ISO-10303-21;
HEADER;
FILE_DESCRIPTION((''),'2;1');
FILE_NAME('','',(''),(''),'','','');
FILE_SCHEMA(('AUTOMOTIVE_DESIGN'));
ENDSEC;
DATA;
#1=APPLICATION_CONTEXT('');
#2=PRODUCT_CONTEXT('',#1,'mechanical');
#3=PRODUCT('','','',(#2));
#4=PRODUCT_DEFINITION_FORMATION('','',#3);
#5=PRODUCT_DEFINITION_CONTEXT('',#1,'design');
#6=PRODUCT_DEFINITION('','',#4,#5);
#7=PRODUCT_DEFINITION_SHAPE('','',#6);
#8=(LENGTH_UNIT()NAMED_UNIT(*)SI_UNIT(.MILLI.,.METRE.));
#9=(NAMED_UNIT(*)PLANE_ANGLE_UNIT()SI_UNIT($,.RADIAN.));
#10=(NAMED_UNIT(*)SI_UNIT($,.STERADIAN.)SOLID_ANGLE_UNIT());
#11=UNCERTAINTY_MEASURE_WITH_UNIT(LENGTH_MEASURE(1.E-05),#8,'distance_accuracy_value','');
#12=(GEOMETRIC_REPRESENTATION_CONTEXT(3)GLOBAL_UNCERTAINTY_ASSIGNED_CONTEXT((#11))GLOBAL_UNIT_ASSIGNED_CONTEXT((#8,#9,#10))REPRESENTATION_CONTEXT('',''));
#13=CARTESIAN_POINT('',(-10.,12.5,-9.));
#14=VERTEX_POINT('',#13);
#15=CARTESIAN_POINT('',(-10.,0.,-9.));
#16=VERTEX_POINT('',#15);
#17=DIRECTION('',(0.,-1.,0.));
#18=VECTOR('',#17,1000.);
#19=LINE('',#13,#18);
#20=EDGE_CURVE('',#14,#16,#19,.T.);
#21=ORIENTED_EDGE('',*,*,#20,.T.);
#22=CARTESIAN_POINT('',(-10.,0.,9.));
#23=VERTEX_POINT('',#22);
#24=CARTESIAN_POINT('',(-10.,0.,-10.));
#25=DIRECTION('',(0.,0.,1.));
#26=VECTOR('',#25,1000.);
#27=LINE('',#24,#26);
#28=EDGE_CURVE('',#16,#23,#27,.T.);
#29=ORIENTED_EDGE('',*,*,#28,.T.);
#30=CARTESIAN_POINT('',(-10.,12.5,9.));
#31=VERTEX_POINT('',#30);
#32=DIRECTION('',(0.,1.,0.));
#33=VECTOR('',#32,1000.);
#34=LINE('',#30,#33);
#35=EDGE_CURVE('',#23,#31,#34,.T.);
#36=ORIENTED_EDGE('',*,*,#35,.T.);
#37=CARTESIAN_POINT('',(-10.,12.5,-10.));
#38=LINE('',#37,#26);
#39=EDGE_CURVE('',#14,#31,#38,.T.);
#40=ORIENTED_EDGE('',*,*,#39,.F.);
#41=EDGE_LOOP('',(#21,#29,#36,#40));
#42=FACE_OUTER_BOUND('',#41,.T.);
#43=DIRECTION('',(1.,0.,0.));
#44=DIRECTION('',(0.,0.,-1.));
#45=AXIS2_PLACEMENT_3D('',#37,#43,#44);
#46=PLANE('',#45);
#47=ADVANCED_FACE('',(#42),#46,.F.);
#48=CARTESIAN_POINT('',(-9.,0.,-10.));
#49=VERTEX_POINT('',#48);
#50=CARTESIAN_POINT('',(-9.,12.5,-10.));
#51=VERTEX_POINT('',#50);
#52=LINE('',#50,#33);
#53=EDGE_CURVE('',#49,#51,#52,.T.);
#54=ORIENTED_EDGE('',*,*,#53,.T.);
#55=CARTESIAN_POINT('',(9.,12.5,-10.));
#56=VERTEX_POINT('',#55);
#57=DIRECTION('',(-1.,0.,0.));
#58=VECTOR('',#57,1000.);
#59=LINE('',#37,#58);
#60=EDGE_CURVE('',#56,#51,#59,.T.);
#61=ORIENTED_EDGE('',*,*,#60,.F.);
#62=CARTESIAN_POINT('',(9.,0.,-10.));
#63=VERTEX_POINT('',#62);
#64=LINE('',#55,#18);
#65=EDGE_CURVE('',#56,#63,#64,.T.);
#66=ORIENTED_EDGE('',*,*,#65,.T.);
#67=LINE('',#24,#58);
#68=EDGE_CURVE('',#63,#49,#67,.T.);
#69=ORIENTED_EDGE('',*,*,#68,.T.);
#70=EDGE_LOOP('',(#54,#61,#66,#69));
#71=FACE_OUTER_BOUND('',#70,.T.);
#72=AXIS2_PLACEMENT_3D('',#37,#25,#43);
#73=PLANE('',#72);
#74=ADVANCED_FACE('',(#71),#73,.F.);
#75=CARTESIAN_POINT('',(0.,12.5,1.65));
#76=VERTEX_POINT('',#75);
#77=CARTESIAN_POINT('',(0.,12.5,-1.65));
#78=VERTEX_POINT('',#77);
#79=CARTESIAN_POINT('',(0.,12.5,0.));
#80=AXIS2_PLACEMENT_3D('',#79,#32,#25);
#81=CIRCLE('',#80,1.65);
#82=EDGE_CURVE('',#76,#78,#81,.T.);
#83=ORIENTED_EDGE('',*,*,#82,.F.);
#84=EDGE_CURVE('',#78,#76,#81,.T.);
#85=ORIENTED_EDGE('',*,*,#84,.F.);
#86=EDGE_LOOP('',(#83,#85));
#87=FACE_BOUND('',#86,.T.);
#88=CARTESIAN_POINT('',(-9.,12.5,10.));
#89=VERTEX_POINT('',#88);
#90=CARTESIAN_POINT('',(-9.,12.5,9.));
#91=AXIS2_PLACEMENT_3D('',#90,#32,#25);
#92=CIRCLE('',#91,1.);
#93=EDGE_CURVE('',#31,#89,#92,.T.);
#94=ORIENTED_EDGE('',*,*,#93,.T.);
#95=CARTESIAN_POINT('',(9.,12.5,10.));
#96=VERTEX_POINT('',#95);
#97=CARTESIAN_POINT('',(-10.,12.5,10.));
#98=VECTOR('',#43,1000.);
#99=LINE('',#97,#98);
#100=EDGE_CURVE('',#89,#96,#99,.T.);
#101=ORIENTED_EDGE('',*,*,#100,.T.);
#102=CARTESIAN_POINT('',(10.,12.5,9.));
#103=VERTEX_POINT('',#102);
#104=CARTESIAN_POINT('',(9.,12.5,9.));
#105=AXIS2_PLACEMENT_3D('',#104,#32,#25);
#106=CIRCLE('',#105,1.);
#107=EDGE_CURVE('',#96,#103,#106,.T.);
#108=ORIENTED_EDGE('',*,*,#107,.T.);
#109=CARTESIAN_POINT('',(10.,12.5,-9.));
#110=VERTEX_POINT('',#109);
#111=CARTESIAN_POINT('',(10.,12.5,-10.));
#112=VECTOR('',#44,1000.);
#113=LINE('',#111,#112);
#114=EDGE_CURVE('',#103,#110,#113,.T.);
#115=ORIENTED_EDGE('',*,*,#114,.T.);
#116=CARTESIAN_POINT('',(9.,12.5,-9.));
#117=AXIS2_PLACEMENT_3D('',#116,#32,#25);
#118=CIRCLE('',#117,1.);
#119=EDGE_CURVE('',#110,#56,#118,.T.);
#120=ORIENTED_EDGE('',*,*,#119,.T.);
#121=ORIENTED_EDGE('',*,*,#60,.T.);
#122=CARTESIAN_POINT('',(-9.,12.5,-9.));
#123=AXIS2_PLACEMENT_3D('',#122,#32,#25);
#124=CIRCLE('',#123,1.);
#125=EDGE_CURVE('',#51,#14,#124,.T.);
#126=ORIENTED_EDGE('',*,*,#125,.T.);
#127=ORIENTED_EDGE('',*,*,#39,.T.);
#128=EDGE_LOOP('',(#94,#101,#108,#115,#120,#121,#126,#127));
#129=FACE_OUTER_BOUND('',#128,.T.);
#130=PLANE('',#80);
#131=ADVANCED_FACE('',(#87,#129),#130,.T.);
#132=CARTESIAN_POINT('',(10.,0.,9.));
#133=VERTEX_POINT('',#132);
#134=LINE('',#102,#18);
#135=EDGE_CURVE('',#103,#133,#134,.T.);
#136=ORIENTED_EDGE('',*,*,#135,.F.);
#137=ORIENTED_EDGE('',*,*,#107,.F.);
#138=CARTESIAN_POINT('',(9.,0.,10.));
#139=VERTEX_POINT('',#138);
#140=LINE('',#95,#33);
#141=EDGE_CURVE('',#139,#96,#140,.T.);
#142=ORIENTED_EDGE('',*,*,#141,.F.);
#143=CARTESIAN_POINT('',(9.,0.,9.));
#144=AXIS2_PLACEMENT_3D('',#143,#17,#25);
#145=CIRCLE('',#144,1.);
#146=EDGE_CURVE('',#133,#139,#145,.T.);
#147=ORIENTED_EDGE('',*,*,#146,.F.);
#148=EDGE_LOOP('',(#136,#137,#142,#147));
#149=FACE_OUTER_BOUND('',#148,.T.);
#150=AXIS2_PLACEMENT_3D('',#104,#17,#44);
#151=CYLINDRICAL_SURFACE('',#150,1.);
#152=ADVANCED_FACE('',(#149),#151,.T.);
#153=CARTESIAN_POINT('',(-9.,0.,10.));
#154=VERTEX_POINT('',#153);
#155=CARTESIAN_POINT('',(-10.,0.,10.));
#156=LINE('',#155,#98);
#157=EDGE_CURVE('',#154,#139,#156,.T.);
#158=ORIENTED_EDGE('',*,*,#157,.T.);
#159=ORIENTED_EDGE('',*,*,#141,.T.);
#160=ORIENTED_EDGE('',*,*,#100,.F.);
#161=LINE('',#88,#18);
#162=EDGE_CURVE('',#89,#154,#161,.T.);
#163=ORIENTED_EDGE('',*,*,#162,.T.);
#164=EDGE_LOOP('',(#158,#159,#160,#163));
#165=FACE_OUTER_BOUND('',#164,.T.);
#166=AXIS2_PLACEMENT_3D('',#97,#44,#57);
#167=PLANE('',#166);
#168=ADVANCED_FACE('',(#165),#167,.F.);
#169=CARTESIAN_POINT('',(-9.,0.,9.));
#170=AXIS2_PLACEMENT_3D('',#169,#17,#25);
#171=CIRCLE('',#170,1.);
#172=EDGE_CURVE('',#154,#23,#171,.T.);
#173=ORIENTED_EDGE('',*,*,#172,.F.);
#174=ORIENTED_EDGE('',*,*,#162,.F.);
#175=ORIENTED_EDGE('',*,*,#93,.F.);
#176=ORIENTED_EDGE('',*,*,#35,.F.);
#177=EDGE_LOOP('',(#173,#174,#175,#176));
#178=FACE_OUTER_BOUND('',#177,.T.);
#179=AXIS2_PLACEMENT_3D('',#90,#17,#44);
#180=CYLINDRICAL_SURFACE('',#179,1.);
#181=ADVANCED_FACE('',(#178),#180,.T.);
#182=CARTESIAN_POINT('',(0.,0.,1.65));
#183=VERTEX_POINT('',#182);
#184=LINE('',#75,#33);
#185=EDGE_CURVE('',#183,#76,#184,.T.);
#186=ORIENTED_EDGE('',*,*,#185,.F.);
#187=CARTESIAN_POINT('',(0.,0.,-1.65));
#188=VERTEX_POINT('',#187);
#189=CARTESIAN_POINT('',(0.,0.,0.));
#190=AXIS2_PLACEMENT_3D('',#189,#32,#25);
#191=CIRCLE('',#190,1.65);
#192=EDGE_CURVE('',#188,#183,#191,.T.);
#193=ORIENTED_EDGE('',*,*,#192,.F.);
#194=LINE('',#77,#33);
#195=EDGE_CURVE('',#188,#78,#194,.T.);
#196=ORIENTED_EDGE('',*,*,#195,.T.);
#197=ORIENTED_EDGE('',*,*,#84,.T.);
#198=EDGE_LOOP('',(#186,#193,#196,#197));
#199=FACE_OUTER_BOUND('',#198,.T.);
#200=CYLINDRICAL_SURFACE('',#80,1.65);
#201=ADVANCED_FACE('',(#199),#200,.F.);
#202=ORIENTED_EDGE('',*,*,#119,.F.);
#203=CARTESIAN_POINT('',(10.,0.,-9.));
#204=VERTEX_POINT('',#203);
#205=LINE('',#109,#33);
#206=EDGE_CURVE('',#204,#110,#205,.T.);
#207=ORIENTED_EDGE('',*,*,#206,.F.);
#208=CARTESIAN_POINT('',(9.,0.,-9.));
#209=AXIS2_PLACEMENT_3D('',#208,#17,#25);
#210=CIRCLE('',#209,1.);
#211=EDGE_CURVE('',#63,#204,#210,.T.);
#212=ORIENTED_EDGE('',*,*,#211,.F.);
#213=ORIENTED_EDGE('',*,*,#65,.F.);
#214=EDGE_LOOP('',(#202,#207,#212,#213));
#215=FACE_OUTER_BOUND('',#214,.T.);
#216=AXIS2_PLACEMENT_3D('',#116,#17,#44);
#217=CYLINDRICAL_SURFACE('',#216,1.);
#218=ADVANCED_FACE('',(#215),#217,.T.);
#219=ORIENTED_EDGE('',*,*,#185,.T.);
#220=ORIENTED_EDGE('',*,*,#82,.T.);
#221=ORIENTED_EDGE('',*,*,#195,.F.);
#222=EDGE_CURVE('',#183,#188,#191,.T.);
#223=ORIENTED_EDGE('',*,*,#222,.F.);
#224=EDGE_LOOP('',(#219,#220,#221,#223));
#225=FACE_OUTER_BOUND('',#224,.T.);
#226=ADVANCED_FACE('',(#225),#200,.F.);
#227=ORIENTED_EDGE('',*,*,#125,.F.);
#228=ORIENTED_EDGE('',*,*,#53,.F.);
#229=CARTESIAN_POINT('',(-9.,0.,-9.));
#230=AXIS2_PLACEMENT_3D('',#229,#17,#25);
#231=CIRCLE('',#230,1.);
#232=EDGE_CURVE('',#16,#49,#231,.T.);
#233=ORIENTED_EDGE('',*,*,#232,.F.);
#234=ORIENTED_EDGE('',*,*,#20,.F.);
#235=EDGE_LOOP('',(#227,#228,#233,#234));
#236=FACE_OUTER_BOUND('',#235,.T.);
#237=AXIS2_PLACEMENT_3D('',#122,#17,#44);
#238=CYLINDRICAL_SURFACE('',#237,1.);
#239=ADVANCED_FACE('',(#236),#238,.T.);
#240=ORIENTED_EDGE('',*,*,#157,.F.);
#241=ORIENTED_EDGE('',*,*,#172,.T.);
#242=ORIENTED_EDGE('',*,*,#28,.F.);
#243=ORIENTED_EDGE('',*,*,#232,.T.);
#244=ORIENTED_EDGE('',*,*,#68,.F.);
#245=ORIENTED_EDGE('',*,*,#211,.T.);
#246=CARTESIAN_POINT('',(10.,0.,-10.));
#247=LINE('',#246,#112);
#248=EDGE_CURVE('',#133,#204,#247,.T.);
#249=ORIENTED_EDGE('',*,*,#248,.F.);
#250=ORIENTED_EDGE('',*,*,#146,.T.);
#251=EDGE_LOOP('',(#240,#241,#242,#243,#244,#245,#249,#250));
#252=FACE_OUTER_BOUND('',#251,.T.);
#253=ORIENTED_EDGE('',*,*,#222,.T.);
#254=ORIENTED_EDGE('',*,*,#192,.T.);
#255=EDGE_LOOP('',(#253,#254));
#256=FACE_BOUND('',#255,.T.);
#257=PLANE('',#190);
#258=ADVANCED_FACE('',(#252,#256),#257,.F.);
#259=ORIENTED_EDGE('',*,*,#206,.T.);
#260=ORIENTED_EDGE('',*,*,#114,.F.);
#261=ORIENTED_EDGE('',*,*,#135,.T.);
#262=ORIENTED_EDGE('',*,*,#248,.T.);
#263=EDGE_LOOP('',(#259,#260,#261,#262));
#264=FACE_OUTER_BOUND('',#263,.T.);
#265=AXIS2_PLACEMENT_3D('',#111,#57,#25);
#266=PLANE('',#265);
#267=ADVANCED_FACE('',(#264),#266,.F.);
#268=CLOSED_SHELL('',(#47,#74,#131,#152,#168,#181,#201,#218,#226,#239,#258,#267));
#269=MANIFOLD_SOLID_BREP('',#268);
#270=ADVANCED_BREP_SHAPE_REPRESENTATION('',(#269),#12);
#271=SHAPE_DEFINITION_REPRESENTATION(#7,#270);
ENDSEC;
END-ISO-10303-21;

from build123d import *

# Parameters (mm, degrees)
SKETCH1_W           = 20
SKETCH1_H           = 20
BOSS_EXTRUDE1_DEPTH = 12.5
M4_TAPPED_HOLE1_D   = 3.3
FILLET1_R           = 1


with BuildPart() as part:
    # Sketch1 → Boss-Extrude1 (new body)
    with BuildSketch(Plane(origin=(0, 0, 0), x_dir=(1, 0, 0), z_dir=(0, 1, 0))):
        Rectangle(SKETCH1_W, SKETCH1_H)
    extrude(amount=BOSS_EXTRUDE1_DEPTH)

    # M4 Tapped Hole1 (through all)
    with Locations(Plane(origin=(0, 12.5, 0), x_dir=(1, 0, 0), z_dir=(0, 1, 0))):
        with Locations((0, 0)):
            Hole(M4_TAPPED_HOLE1_D / 2)

    # Fillet1
    fillet1_edges = [part.edges().sort_by_distance(p)[0] for p in [
        (10, 6.25, 10),
        (-10, 6.25, 10),
        (-10, 6.25, -10),
        (10, 6.25, -10),
    ]]
    fillet(fillet1_edges, radius=FILLET1_R)


solid = part.part
